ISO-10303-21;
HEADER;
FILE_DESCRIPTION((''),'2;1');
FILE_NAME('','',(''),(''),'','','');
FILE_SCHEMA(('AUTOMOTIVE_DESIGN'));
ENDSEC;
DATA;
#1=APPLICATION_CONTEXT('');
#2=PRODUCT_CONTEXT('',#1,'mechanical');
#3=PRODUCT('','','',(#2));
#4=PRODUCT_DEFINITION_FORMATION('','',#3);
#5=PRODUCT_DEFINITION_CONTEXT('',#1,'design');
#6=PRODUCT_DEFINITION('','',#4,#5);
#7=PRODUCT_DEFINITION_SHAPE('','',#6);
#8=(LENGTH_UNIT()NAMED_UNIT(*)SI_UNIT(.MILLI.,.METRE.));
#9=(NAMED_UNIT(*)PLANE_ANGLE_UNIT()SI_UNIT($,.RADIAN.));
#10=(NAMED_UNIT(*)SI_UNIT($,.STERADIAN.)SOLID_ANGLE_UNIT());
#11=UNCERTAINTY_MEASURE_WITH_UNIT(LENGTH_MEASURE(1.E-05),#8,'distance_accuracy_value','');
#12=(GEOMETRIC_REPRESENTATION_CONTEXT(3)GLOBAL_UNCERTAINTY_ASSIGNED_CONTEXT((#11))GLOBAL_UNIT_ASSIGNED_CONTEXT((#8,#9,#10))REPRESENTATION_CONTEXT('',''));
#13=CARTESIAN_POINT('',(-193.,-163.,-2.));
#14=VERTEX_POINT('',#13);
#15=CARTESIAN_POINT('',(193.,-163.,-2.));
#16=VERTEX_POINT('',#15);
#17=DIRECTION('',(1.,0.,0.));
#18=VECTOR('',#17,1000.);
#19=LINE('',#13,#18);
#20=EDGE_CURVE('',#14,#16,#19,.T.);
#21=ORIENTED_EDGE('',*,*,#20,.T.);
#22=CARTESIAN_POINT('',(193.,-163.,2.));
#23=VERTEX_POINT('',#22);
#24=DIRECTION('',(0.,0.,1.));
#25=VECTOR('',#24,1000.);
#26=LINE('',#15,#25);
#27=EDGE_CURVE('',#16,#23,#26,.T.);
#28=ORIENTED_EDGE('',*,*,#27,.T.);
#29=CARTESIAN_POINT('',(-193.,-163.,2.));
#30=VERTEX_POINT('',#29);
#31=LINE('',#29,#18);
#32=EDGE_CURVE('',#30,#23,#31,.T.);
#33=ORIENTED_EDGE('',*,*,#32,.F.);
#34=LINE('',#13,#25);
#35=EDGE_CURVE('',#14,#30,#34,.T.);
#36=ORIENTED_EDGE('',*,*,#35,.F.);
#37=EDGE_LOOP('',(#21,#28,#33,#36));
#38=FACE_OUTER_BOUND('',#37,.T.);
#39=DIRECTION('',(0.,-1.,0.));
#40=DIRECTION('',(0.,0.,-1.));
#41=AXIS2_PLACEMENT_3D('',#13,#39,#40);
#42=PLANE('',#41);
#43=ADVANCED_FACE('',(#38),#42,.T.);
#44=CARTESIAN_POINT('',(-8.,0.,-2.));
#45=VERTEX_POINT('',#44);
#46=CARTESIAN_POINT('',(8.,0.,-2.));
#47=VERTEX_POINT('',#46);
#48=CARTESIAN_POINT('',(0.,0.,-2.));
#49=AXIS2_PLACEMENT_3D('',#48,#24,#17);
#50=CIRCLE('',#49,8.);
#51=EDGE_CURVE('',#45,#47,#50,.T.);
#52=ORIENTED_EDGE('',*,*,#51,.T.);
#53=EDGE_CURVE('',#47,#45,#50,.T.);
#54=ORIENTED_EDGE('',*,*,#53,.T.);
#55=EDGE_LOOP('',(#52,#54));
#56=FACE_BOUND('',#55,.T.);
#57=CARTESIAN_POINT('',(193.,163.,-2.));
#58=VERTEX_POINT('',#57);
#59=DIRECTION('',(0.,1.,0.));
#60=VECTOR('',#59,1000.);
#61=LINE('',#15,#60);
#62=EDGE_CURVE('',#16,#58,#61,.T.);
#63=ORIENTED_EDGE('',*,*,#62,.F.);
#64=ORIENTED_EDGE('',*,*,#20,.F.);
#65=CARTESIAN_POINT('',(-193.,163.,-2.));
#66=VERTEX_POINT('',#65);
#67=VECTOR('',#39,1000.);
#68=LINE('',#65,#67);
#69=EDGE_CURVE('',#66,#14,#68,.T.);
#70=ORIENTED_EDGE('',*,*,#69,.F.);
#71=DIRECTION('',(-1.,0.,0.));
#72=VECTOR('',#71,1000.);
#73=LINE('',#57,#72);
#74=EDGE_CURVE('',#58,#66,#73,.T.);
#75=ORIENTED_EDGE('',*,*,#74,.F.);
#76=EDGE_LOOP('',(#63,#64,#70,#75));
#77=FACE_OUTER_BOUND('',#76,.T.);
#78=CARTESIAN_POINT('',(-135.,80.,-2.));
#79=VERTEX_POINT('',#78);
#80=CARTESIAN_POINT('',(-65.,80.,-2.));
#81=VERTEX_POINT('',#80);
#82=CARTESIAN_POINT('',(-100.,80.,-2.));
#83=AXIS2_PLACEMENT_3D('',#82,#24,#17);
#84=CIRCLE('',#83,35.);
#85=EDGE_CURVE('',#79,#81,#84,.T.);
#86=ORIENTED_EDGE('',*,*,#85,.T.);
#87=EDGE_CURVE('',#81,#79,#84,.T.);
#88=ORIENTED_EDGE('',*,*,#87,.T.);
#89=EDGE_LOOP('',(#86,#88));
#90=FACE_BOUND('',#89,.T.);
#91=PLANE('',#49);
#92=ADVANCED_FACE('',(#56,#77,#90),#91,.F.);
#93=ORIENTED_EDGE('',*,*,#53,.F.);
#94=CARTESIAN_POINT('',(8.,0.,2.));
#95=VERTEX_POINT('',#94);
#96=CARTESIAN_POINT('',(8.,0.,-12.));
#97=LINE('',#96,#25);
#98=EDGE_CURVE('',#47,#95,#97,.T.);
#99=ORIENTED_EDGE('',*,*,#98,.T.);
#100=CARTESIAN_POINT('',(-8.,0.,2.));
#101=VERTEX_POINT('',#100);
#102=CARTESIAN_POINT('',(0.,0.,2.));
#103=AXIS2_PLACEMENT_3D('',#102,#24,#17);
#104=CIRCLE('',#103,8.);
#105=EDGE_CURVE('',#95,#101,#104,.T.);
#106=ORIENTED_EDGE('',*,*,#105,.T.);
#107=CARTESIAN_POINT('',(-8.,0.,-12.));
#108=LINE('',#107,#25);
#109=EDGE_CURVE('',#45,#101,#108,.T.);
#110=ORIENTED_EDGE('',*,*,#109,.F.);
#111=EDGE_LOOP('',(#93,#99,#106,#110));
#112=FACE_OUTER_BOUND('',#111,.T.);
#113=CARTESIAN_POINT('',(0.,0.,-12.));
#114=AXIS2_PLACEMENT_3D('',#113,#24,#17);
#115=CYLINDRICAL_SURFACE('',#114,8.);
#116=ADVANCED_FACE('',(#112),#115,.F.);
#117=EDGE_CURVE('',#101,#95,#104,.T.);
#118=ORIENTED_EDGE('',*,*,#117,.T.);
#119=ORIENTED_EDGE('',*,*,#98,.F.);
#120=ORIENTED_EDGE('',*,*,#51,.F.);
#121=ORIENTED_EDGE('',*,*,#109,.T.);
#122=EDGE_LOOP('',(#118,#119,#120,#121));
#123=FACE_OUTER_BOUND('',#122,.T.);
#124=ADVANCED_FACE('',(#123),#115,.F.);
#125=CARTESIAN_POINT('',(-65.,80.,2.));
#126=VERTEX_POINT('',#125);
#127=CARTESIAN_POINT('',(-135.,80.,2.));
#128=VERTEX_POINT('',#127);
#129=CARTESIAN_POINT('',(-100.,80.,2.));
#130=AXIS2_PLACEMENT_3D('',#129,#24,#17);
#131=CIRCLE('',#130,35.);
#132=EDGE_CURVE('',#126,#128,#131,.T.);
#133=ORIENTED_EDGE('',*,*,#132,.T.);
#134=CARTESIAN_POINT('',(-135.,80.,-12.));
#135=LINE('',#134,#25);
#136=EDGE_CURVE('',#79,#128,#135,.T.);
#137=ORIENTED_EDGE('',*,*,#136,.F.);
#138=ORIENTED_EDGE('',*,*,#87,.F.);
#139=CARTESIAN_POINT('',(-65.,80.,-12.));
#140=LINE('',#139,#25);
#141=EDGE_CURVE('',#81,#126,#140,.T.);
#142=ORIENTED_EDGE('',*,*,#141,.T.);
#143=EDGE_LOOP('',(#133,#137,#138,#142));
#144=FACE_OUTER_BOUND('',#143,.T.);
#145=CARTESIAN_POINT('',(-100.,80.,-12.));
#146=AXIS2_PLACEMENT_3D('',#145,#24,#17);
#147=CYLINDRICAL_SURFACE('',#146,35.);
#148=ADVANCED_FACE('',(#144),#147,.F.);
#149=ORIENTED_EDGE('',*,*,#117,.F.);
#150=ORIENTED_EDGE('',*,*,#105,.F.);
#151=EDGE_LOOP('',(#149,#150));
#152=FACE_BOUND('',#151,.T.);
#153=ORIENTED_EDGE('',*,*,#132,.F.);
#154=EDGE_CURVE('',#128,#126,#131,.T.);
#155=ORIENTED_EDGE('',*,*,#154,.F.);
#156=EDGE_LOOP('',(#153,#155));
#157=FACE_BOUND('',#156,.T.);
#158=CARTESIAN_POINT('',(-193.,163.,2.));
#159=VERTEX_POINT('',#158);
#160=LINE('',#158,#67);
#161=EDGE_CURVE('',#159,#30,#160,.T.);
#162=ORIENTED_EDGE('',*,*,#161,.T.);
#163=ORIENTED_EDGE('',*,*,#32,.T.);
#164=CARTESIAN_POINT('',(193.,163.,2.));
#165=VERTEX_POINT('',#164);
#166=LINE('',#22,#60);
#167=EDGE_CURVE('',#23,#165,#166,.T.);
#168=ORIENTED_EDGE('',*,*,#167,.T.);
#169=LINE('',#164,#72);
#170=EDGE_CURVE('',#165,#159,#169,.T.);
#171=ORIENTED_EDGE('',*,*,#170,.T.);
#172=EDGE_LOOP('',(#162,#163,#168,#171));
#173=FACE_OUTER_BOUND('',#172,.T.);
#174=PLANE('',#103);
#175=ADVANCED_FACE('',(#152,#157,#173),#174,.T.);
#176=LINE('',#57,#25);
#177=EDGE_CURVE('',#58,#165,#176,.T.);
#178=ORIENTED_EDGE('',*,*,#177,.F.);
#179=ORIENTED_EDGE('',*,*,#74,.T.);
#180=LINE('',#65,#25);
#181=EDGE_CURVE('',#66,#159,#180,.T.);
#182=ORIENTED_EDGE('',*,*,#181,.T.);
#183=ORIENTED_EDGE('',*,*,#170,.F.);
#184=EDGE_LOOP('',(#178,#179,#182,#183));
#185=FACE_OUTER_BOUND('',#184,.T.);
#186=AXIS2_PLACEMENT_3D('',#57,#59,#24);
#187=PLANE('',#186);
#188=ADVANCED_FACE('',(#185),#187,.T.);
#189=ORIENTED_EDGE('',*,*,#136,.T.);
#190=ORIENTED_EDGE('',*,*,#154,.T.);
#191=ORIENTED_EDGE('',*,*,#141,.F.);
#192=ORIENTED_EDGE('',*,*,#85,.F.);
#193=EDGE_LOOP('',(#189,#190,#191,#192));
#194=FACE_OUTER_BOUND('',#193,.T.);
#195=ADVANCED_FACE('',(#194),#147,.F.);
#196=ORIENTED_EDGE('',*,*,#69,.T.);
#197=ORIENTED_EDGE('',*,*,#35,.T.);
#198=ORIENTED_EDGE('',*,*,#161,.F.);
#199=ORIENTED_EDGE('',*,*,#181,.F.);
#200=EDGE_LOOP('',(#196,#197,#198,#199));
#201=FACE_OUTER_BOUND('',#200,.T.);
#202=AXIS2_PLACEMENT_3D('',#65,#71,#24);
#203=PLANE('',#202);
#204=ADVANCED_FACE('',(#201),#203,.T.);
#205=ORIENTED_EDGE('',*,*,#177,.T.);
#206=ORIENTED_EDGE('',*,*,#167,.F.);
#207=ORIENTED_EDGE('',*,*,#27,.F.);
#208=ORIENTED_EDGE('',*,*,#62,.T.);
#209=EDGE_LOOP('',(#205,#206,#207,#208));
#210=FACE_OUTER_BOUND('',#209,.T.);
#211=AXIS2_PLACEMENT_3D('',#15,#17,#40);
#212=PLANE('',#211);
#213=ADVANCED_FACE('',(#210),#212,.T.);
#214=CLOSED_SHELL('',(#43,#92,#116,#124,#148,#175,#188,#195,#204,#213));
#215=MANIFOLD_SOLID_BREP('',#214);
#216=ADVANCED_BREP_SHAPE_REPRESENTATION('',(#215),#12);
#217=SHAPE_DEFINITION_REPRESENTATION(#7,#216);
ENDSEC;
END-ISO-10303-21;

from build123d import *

# Parameters (mm, degrees)
SKETCH_1_W          = 386
SKETCH_1_H          = 326
EXTRUDE_1_DEPTH     = 2
SKETCH_2_R          = 8
SKETCH_2_R_2        = 35
CUT_EXTRUDE_1_DEPTH = 12


with BuildPart() as part:
    # 草图1 → 凸台-拉伸1 (new, symmetric)
    with BuildSketch(Plane.XY):
        Rectangle(SKETCH_1_W, SKETCH_1_H)
    extrude(amount=EXTRUDE_1_DEPTH, both=True)

    # 草图2 → 切除-拉伸1 (cut, symmetric)
    with BuildSketch(Plane.XY):
        Circle(SKETCH_2_R)
        with Locations((-100, 80)):
            Circle(SKETCH_2_R_2)
    extrude(amount=CUT_EXTRUDE_1_DEPTH, both=True, mode=Mode.SUBTRACT)


solid = part.part
